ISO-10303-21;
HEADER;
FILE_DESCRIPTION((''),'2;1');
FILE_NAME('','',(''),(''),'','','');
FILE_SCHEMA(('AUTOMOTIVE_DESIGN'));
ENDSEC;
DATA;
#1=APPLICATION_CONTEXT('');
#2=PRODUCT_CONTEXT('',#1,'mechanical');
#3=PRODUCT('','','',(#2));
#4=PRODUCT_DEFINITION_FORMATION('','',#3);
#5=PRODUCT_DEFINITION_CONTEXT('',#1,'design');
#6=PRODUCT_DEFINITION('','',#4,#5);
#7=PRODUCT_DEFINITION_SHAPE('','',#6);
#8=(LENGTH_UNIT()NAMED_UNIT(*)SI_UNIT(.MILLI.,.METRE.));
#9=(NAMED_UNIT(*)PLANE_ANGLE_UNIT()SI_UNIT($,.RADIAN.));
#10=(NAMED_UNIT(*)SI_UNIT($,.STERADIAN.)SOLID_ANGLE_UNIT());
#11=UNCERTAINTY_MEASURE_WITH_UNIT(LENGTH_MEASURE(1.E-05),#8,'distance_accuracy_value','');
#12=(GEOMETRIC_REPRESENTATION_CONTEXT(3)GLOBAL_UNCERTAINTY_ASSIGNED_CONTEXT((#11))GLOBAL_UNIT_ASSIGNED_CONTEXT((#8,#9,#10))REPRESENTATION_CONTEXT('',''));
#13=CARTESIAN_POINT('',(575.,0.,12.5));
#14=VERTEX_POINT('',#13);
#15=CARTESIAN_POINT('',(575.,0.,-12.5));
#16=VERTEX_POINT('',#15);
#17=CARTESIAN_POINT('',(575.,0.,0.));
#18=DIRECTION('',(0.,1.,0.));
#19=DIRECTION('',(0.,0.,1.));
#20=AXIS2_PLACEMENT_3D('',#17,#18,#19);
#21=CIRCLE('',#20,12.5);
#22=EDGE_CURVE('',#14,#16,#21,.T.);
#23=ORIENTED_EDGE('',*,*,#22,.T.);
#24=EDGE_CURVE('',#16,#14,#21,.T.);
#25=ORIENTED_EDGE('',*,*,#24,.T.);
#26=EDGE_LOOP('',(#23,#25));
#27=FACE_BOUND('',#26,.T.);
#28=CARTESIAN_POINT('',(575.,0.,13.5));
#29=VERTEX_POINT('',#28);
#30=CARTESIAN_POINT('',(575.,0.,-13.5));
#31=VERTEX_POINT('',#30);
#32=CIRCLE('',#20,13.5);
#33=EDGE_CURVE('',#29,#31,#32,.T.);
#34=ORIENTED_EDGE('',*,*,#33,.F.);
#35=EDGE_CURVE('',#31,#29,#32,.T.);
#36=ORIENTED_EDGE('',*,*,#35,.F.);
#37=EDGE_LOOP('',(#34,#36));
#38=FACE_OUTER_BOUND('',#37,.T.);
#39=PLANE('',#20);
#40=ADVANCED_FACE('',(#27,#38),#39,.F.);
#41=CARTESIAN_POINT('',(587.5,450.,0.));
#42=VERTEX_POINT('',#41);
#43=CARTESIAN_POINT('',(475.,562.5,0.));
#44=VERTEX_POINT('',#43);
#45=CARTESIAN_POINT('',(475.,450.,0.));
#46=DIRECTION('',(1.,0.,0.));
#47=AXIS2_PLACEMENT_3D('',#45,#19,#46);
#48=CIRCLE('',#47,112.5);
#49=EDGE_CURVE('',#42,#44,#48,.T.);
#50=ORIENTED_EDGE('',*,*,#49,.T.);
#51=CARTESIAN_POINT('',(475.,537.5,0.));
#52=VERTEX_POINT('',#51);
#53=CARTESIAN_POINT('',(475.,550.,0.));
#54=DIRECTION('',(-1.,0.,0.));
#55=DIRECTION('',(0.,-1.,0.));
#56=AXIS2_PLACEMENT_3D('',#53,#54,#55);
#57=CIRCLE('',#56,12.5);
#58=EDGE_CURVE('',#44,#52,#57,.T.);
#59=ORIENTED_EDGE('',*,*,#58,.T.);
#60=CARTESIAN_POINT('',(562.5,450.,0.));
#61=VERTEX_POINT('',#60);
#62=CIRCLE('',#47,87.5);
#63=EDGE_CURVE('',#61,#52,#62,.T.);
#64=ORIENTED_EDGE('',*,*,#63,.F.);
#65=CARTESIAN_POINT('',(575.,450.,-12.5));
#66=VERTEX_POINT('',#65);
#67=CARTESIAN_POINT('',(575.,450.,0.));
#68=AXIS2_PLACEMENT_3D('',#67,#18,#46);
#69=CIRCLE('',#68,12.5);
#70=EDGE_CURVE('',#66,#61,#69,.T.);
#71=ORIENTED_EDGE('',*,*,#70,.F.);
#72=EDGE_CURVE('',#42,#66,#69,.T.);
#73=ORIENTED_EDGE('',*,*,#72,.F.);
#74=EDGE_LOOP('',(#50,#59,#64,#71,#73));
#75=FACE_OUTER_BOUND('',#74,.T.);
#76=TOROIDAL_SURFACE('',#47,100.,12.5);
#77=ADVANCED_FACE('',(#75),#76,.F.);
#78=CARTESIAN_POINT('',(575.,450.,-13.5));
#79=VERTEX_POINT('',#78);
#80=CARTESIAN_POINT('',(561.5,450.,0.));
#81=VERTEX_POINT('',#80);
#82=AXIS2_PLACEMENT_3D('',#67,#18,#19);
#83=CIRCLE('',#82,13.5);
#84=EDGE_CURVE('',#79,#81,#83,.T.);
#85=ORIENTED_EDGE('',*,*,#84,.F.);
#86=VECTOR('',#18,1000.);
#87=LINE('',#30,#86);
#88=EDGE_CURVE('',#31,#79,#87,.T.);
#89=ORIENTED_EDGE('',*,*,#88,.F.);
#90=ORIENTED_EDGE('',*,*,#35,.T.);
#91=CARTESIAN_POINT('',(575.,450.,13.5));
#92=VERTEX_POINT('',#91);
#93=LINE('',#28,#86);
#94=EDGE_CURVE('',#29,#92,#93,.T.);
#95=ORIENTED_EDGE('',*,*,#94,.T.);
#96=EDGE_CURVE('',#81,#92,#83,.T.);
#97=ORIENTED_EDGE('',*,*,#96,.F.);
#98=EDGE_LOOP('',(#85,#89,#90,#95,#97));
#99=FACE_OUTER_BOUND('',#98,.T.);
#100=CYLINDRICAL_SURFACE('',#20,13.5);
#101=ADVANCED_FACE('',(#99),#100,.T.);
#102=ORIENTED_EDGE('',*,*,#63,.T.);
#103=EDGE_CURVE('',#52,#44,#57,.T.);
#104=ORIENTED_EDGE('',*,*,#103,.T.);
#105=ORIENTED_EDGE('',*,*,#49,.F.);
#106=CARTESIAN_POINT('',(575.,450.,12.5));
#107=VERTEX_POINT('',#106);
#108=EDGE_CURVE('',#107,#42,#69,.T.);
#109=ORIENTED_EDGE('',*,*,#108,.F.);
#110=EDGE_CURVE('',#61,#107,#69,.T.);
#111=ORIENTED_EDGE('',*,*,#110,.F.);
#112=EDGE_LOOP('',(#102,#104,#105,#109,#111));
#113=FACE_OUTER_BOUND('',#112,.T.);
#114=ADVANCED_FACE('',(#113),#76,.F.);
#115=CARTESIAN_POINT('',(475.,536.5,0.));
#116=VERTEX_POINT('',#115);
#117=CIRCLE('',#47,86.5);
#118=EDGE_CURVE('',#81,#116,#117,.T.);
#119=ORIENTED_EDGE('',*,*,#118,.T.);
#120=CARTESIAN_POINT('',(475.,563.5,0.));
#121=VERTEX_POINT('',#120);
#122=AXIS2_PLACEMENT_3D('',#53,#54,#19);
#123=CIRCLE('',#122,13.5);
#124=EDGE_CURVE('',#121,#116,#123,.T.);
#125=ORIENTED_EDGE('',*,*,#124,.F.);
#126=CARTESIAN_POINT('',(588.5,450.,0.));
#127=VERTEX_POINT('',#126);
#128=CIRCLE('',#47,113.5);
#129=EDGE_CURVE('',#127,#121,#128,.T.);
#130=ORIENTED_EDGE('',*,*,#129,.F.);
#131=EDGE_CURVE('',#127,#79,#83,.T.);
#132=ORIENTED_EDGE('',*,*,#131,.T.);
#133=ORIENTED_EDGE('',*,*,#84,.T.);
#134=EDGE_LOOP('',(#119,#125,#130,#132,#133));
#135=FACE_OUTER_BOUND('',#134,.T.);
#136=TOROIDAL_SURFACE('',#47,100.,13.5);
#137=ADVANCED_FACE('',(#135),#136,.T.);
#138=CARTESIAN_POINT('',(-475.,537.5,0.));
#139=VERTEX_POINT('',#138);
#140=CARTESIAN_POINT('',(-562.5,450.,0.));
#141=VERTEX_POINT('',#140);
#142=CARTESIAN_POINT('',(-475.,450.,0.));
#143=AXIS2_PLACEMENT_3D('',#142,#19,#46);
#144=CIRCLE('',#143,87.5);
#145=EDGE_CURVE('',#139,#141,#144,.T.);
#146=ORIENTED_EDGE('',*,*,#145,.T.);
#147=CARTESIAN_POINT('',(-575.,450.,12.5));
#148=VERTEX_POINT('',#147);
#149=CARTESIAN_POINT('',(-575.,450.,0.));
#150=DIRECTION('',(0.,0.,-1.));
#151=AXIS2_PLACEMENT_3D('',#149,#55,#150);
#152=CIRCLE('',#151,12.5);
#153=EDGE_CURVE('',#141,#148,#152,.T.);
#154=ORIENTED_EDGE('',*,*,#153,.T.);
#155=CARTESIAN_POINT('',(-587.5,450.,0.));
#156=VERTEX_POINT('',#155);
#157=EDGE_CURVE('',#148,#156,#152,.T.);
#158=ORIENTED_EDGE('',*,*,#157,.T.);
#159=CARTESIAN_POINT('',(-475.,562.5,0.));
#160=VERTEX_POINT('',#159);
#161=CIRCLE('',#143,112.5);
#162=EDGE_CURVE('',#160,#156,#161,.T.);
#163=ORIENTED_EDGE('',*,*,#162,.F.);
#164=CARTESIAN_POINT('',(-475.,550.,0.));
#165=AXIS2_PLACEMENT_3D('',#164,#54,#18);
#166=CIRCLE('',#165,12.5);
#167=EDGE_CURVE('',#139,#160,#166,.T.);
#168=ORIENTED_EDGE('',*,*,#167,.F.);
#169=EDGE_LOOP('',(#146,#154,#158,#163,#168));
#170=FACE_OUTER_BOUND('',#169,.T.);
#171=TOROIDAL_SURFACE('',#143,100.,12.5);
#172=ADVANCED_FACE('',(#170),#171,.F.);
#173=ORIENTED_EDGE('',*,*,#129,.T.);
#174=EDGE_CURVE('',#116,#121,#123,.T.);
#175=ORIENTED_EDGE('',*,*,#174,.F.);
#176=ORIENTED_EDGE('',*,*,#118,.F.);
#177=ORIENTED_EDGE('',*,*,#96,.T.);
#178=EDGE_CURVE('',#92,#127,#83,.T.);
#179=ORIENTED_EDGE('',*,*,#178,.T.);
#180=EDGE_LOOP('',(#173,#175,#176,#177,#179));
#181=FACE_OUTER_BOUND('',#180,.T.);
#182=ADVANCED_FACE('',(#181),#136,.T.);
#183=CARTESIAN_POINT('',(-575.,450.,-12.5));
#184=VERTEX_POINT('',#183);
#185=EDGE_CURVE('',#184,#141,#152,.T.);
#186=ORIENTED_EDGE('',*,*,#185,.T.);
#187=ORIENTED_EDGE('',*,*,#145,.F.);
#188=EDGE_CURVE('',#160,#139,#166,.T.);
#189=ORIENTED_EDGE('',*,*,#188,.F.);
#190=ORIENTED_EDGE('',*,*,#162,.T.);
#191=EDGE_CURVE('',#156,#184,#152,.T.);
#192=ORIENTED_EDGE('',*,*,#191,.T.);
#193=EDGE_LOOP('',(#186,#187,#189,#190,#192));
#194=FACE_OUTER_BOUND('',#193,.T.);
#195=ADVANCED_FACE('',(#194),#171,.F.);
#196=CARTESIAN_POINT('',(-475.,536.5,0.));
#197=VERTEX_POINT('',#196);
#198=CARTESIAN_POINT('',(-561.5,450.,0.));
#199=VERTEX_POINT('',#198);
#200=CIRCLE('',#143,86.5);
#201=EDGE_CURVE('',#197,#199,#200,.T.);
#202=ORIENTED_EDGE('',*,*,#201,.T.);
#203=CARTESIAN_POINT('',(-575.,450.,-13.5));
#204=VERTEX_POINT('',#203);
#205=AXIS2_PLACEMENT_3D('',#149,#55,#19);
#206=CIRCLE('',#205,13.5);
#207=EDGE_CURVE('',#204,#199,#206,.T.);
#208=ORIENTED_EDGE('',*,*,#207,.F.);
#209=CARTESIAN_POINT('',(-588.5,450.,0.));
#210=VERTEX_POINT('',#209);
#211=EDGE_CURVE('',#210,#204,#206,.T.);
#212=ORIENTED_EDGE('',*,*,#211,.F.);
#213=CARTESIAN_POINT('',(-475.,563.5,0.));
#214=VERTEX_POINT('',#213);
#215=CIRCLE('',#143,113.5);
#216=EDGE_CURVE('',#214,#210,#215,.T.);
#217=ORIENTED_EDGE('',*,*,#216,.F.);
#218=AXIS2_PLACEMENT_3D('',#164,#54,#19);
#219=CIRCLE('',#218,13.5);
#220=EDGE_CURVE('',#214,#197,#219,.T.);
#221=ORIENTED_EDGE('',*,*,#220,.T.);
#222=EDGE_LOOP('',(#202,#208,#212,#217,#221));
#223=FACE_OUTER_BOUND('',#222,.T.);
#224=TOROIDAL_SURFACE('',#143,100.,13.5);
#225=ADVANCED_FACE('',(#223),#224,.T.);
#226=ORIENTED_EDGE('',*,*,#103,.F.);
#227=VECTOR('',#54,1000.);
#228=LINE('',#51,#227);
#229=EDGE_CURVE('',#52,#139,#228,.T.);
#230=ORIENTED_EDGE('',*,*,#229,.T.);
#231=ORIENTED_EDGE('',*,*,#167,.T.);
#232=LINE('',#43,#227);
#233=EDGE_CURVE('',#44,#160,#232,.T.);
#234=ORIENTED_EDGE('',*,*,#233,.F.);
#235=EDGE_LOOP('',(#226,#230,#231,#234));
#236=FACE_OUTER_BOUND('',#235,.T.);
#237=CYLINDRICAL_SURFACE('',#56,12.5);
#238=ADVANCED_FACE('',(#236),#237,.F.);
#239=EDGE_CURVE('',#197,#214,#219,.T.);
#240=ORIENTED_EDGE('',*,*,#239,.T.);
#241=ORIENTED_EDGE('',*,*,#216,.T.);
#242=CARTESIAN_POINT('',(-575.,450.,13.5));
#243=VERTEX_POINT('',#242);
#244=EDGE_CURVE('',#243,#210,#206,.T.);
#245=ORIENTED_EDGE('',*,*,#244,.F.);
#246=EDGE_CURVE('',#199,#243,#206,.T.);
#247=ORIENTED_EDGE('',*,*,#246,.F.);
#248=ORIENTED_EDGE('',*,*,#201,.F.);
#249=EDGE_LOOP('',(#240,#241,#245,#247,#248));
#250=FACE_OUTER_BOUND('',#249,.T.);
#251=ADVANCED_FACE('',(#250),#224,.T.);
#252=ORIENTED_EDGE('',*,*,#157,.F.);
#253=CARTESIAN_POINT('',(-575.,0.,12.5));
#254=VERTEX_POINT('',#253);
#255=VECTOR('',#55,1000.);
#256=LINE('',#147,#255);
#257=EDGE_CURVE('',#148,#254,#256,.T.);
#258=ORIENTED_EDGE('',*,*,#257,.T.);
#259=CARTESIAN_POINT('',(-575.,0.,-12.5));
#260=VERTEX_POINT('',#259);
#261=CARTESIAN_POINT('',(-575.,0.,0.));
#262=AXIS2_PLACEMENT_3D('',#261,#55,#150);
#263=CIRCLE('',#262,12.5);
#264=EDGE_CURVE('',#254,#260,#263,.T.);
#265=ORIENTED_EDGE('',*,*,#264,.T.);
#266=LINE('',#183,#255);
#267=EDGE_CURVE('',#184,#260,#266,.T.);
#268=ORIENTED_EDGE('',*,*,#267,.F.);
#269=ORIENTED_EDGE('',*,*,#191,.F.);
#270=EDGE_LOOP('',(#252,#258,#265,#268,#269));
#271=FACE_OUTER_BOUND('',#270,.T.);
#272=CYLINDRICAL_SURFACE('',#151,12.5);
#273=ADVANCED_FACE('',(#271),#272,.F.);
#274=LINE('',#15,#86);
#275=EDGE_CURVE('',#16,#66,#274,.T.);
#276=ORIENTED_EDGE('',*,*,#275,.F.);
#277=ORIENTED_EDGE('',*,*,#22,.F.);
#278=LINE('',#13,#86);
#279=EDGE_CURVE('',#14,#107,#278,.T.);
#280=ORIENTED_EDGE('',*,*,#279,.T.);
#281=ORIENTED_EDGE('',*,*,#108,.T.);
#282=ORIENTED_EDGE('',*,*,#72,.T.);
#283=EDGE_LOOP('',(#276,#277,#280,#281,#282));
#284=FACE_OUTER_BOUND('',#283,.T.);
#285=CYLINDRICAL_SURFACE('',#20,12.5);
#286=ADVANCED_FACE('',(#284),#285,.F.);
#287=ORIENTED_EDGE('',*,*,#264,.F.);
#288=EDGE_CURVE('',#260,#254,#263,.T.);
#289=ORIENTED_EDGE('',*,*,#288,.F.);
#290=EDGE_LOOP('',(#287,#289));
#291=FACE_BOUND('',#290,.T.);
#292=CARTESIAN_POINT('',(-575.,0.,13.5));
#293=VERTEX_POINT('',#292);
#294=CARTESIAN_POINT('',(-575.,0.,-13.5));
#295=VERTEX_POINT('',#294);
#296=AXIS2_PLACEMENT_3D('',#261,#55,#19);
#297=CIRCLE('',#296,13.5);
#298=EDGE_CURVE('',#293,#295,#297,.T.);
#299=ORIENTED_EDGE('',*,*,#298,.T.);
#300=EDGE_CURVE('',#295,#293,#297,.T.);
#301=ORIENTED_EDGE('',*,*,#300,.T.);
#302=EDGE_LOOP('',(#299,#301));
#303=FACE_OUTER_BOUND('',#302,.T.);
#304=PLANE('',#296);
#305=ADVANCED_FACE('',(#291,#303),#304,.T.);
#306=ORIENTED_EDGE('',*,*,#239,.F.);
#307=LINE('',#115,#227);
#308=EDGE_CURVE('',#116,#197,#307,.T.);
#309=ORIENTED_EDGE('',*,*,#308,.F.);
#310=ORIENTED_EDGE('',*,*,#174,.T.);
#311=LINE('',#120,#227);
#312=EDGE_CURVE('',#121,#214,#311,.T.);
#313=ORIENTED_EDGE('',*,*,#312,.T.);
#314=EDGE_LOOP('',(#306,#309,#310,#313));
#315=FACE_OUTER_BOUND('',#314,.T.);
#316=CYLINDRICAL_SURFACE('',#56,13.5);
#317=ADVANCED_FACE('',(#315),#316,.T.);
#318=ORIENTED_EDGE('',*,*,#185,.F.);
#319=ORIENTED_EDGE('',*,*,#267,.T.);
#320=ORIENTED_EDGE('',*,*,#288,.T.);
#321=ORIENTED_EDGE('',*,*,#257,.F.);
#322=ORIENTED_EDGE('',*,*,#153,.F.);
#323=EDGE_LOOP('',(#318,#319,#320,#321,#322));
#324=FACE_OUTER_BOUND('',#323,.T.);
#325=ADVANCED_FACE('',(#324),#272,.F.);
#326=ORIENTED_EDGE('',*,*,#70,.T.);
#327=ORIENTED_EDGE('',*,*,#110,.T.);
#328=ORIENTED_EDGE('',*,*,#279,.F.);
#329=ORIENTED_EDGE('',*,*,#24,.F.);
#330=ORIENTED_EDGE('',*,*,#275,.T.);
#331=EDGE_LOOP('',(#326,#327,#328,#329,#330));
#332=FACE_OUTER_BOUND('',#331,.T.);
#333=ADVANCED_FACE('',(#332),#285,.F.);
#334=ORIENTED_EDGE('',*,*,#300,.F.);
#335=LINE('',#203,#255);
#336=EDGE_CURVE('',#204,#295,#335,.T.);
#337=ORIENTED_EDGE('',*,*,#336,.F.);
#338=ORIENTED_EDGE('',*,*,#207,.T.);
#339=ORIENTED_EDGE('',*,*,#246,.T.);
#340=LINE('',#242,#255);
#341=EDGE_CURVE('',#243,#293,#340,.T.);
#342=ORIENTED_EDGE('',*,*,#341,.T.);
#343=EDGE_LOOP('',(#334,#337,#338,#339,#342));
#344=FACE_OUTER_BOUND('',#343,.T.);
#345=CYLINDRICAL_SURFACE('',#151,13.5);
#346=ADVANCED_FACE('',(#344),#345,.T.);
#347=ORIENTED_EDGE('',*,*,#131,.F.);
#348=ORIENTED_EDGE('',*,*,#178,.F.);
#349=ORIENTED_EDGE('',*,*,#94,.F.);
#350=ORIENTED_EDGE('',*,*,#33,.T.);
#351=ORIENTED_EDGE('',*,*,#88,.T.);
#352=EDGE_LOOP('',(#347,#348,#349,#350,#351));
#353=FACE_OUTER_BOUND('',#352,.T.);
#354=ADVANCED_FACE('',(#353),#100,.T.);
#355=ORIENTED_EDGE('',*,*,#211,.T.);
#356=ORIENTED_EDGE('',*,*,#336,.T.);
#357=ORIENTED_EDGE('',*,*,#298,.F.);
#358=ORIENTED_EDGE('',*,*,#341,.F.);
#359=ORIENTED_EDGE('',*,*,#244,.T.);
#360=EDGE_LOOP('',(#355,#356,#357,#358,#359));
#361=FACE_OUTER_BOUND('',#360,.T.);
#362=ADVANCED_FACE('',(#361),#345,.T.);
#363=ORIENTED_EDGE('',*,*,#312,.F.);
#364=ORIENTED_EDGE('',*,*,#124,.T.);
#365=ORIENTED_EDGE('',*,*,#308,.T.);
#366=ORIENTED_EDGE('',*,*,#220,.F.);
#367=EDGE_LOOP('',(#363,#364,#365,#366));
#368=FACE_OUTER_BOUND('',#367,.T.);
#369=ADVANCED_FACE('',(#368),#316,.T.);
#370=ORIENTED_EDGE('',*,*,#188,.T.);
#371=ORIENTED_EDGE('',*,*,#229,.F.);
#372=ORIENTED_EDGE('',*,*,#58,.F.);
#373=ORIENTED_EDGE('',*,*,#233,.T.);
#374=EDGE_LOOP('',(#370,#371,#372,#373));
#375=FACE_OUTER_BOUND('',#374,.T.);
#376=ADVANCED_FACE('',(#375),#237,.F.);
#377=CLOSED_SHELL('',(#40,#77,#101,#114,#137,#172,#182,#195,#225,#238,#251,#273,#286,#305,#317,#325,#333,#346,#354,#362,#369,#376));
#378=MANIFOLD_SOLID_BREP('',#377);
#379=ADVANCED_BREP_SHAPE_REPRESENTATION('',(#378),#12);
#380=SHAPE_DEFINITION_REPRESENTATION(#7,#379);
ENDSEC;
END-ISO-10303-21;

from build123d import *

# Parameters (mm, degrees)
SWEEP_1_PROFILE_R   = 13.5
SWEEP_1_PROFILE_R_2 = 12.5


with BuildPart() as part:
    # 扫描-薄件1: sweep along a path in 草图1
    with BuildLine(Plane.XY) as sweep_1_path:
        Line((-575, 0), (-575, 450))
        ThreePointArc((-575, 450), (-545.710678119, 520.710678119), (-475, 550))
        Line((-475, 550), (475, 550))
        ThreePointArc((475, 550), (545.710678119, 520.710678119), (575, 450))
        Line((575, 450), (575, 0))
    # 扫描-薄件1 profile (on start of the path) → 扫描-薄件1 (sweep)
    with BuildSketch(Plane(origin=(-575, 0, 0), x_dir=(0, 0, 1), z_dir=(0, 1, 0))):
        Circle(SWEEP_1_PROFILE_R)
        Circle(SWEEP_1_PROFILE_R_2, mode=Mode.SUBTRACT)
    sweep(path=sweep_1_path.line)


solid = part.part
